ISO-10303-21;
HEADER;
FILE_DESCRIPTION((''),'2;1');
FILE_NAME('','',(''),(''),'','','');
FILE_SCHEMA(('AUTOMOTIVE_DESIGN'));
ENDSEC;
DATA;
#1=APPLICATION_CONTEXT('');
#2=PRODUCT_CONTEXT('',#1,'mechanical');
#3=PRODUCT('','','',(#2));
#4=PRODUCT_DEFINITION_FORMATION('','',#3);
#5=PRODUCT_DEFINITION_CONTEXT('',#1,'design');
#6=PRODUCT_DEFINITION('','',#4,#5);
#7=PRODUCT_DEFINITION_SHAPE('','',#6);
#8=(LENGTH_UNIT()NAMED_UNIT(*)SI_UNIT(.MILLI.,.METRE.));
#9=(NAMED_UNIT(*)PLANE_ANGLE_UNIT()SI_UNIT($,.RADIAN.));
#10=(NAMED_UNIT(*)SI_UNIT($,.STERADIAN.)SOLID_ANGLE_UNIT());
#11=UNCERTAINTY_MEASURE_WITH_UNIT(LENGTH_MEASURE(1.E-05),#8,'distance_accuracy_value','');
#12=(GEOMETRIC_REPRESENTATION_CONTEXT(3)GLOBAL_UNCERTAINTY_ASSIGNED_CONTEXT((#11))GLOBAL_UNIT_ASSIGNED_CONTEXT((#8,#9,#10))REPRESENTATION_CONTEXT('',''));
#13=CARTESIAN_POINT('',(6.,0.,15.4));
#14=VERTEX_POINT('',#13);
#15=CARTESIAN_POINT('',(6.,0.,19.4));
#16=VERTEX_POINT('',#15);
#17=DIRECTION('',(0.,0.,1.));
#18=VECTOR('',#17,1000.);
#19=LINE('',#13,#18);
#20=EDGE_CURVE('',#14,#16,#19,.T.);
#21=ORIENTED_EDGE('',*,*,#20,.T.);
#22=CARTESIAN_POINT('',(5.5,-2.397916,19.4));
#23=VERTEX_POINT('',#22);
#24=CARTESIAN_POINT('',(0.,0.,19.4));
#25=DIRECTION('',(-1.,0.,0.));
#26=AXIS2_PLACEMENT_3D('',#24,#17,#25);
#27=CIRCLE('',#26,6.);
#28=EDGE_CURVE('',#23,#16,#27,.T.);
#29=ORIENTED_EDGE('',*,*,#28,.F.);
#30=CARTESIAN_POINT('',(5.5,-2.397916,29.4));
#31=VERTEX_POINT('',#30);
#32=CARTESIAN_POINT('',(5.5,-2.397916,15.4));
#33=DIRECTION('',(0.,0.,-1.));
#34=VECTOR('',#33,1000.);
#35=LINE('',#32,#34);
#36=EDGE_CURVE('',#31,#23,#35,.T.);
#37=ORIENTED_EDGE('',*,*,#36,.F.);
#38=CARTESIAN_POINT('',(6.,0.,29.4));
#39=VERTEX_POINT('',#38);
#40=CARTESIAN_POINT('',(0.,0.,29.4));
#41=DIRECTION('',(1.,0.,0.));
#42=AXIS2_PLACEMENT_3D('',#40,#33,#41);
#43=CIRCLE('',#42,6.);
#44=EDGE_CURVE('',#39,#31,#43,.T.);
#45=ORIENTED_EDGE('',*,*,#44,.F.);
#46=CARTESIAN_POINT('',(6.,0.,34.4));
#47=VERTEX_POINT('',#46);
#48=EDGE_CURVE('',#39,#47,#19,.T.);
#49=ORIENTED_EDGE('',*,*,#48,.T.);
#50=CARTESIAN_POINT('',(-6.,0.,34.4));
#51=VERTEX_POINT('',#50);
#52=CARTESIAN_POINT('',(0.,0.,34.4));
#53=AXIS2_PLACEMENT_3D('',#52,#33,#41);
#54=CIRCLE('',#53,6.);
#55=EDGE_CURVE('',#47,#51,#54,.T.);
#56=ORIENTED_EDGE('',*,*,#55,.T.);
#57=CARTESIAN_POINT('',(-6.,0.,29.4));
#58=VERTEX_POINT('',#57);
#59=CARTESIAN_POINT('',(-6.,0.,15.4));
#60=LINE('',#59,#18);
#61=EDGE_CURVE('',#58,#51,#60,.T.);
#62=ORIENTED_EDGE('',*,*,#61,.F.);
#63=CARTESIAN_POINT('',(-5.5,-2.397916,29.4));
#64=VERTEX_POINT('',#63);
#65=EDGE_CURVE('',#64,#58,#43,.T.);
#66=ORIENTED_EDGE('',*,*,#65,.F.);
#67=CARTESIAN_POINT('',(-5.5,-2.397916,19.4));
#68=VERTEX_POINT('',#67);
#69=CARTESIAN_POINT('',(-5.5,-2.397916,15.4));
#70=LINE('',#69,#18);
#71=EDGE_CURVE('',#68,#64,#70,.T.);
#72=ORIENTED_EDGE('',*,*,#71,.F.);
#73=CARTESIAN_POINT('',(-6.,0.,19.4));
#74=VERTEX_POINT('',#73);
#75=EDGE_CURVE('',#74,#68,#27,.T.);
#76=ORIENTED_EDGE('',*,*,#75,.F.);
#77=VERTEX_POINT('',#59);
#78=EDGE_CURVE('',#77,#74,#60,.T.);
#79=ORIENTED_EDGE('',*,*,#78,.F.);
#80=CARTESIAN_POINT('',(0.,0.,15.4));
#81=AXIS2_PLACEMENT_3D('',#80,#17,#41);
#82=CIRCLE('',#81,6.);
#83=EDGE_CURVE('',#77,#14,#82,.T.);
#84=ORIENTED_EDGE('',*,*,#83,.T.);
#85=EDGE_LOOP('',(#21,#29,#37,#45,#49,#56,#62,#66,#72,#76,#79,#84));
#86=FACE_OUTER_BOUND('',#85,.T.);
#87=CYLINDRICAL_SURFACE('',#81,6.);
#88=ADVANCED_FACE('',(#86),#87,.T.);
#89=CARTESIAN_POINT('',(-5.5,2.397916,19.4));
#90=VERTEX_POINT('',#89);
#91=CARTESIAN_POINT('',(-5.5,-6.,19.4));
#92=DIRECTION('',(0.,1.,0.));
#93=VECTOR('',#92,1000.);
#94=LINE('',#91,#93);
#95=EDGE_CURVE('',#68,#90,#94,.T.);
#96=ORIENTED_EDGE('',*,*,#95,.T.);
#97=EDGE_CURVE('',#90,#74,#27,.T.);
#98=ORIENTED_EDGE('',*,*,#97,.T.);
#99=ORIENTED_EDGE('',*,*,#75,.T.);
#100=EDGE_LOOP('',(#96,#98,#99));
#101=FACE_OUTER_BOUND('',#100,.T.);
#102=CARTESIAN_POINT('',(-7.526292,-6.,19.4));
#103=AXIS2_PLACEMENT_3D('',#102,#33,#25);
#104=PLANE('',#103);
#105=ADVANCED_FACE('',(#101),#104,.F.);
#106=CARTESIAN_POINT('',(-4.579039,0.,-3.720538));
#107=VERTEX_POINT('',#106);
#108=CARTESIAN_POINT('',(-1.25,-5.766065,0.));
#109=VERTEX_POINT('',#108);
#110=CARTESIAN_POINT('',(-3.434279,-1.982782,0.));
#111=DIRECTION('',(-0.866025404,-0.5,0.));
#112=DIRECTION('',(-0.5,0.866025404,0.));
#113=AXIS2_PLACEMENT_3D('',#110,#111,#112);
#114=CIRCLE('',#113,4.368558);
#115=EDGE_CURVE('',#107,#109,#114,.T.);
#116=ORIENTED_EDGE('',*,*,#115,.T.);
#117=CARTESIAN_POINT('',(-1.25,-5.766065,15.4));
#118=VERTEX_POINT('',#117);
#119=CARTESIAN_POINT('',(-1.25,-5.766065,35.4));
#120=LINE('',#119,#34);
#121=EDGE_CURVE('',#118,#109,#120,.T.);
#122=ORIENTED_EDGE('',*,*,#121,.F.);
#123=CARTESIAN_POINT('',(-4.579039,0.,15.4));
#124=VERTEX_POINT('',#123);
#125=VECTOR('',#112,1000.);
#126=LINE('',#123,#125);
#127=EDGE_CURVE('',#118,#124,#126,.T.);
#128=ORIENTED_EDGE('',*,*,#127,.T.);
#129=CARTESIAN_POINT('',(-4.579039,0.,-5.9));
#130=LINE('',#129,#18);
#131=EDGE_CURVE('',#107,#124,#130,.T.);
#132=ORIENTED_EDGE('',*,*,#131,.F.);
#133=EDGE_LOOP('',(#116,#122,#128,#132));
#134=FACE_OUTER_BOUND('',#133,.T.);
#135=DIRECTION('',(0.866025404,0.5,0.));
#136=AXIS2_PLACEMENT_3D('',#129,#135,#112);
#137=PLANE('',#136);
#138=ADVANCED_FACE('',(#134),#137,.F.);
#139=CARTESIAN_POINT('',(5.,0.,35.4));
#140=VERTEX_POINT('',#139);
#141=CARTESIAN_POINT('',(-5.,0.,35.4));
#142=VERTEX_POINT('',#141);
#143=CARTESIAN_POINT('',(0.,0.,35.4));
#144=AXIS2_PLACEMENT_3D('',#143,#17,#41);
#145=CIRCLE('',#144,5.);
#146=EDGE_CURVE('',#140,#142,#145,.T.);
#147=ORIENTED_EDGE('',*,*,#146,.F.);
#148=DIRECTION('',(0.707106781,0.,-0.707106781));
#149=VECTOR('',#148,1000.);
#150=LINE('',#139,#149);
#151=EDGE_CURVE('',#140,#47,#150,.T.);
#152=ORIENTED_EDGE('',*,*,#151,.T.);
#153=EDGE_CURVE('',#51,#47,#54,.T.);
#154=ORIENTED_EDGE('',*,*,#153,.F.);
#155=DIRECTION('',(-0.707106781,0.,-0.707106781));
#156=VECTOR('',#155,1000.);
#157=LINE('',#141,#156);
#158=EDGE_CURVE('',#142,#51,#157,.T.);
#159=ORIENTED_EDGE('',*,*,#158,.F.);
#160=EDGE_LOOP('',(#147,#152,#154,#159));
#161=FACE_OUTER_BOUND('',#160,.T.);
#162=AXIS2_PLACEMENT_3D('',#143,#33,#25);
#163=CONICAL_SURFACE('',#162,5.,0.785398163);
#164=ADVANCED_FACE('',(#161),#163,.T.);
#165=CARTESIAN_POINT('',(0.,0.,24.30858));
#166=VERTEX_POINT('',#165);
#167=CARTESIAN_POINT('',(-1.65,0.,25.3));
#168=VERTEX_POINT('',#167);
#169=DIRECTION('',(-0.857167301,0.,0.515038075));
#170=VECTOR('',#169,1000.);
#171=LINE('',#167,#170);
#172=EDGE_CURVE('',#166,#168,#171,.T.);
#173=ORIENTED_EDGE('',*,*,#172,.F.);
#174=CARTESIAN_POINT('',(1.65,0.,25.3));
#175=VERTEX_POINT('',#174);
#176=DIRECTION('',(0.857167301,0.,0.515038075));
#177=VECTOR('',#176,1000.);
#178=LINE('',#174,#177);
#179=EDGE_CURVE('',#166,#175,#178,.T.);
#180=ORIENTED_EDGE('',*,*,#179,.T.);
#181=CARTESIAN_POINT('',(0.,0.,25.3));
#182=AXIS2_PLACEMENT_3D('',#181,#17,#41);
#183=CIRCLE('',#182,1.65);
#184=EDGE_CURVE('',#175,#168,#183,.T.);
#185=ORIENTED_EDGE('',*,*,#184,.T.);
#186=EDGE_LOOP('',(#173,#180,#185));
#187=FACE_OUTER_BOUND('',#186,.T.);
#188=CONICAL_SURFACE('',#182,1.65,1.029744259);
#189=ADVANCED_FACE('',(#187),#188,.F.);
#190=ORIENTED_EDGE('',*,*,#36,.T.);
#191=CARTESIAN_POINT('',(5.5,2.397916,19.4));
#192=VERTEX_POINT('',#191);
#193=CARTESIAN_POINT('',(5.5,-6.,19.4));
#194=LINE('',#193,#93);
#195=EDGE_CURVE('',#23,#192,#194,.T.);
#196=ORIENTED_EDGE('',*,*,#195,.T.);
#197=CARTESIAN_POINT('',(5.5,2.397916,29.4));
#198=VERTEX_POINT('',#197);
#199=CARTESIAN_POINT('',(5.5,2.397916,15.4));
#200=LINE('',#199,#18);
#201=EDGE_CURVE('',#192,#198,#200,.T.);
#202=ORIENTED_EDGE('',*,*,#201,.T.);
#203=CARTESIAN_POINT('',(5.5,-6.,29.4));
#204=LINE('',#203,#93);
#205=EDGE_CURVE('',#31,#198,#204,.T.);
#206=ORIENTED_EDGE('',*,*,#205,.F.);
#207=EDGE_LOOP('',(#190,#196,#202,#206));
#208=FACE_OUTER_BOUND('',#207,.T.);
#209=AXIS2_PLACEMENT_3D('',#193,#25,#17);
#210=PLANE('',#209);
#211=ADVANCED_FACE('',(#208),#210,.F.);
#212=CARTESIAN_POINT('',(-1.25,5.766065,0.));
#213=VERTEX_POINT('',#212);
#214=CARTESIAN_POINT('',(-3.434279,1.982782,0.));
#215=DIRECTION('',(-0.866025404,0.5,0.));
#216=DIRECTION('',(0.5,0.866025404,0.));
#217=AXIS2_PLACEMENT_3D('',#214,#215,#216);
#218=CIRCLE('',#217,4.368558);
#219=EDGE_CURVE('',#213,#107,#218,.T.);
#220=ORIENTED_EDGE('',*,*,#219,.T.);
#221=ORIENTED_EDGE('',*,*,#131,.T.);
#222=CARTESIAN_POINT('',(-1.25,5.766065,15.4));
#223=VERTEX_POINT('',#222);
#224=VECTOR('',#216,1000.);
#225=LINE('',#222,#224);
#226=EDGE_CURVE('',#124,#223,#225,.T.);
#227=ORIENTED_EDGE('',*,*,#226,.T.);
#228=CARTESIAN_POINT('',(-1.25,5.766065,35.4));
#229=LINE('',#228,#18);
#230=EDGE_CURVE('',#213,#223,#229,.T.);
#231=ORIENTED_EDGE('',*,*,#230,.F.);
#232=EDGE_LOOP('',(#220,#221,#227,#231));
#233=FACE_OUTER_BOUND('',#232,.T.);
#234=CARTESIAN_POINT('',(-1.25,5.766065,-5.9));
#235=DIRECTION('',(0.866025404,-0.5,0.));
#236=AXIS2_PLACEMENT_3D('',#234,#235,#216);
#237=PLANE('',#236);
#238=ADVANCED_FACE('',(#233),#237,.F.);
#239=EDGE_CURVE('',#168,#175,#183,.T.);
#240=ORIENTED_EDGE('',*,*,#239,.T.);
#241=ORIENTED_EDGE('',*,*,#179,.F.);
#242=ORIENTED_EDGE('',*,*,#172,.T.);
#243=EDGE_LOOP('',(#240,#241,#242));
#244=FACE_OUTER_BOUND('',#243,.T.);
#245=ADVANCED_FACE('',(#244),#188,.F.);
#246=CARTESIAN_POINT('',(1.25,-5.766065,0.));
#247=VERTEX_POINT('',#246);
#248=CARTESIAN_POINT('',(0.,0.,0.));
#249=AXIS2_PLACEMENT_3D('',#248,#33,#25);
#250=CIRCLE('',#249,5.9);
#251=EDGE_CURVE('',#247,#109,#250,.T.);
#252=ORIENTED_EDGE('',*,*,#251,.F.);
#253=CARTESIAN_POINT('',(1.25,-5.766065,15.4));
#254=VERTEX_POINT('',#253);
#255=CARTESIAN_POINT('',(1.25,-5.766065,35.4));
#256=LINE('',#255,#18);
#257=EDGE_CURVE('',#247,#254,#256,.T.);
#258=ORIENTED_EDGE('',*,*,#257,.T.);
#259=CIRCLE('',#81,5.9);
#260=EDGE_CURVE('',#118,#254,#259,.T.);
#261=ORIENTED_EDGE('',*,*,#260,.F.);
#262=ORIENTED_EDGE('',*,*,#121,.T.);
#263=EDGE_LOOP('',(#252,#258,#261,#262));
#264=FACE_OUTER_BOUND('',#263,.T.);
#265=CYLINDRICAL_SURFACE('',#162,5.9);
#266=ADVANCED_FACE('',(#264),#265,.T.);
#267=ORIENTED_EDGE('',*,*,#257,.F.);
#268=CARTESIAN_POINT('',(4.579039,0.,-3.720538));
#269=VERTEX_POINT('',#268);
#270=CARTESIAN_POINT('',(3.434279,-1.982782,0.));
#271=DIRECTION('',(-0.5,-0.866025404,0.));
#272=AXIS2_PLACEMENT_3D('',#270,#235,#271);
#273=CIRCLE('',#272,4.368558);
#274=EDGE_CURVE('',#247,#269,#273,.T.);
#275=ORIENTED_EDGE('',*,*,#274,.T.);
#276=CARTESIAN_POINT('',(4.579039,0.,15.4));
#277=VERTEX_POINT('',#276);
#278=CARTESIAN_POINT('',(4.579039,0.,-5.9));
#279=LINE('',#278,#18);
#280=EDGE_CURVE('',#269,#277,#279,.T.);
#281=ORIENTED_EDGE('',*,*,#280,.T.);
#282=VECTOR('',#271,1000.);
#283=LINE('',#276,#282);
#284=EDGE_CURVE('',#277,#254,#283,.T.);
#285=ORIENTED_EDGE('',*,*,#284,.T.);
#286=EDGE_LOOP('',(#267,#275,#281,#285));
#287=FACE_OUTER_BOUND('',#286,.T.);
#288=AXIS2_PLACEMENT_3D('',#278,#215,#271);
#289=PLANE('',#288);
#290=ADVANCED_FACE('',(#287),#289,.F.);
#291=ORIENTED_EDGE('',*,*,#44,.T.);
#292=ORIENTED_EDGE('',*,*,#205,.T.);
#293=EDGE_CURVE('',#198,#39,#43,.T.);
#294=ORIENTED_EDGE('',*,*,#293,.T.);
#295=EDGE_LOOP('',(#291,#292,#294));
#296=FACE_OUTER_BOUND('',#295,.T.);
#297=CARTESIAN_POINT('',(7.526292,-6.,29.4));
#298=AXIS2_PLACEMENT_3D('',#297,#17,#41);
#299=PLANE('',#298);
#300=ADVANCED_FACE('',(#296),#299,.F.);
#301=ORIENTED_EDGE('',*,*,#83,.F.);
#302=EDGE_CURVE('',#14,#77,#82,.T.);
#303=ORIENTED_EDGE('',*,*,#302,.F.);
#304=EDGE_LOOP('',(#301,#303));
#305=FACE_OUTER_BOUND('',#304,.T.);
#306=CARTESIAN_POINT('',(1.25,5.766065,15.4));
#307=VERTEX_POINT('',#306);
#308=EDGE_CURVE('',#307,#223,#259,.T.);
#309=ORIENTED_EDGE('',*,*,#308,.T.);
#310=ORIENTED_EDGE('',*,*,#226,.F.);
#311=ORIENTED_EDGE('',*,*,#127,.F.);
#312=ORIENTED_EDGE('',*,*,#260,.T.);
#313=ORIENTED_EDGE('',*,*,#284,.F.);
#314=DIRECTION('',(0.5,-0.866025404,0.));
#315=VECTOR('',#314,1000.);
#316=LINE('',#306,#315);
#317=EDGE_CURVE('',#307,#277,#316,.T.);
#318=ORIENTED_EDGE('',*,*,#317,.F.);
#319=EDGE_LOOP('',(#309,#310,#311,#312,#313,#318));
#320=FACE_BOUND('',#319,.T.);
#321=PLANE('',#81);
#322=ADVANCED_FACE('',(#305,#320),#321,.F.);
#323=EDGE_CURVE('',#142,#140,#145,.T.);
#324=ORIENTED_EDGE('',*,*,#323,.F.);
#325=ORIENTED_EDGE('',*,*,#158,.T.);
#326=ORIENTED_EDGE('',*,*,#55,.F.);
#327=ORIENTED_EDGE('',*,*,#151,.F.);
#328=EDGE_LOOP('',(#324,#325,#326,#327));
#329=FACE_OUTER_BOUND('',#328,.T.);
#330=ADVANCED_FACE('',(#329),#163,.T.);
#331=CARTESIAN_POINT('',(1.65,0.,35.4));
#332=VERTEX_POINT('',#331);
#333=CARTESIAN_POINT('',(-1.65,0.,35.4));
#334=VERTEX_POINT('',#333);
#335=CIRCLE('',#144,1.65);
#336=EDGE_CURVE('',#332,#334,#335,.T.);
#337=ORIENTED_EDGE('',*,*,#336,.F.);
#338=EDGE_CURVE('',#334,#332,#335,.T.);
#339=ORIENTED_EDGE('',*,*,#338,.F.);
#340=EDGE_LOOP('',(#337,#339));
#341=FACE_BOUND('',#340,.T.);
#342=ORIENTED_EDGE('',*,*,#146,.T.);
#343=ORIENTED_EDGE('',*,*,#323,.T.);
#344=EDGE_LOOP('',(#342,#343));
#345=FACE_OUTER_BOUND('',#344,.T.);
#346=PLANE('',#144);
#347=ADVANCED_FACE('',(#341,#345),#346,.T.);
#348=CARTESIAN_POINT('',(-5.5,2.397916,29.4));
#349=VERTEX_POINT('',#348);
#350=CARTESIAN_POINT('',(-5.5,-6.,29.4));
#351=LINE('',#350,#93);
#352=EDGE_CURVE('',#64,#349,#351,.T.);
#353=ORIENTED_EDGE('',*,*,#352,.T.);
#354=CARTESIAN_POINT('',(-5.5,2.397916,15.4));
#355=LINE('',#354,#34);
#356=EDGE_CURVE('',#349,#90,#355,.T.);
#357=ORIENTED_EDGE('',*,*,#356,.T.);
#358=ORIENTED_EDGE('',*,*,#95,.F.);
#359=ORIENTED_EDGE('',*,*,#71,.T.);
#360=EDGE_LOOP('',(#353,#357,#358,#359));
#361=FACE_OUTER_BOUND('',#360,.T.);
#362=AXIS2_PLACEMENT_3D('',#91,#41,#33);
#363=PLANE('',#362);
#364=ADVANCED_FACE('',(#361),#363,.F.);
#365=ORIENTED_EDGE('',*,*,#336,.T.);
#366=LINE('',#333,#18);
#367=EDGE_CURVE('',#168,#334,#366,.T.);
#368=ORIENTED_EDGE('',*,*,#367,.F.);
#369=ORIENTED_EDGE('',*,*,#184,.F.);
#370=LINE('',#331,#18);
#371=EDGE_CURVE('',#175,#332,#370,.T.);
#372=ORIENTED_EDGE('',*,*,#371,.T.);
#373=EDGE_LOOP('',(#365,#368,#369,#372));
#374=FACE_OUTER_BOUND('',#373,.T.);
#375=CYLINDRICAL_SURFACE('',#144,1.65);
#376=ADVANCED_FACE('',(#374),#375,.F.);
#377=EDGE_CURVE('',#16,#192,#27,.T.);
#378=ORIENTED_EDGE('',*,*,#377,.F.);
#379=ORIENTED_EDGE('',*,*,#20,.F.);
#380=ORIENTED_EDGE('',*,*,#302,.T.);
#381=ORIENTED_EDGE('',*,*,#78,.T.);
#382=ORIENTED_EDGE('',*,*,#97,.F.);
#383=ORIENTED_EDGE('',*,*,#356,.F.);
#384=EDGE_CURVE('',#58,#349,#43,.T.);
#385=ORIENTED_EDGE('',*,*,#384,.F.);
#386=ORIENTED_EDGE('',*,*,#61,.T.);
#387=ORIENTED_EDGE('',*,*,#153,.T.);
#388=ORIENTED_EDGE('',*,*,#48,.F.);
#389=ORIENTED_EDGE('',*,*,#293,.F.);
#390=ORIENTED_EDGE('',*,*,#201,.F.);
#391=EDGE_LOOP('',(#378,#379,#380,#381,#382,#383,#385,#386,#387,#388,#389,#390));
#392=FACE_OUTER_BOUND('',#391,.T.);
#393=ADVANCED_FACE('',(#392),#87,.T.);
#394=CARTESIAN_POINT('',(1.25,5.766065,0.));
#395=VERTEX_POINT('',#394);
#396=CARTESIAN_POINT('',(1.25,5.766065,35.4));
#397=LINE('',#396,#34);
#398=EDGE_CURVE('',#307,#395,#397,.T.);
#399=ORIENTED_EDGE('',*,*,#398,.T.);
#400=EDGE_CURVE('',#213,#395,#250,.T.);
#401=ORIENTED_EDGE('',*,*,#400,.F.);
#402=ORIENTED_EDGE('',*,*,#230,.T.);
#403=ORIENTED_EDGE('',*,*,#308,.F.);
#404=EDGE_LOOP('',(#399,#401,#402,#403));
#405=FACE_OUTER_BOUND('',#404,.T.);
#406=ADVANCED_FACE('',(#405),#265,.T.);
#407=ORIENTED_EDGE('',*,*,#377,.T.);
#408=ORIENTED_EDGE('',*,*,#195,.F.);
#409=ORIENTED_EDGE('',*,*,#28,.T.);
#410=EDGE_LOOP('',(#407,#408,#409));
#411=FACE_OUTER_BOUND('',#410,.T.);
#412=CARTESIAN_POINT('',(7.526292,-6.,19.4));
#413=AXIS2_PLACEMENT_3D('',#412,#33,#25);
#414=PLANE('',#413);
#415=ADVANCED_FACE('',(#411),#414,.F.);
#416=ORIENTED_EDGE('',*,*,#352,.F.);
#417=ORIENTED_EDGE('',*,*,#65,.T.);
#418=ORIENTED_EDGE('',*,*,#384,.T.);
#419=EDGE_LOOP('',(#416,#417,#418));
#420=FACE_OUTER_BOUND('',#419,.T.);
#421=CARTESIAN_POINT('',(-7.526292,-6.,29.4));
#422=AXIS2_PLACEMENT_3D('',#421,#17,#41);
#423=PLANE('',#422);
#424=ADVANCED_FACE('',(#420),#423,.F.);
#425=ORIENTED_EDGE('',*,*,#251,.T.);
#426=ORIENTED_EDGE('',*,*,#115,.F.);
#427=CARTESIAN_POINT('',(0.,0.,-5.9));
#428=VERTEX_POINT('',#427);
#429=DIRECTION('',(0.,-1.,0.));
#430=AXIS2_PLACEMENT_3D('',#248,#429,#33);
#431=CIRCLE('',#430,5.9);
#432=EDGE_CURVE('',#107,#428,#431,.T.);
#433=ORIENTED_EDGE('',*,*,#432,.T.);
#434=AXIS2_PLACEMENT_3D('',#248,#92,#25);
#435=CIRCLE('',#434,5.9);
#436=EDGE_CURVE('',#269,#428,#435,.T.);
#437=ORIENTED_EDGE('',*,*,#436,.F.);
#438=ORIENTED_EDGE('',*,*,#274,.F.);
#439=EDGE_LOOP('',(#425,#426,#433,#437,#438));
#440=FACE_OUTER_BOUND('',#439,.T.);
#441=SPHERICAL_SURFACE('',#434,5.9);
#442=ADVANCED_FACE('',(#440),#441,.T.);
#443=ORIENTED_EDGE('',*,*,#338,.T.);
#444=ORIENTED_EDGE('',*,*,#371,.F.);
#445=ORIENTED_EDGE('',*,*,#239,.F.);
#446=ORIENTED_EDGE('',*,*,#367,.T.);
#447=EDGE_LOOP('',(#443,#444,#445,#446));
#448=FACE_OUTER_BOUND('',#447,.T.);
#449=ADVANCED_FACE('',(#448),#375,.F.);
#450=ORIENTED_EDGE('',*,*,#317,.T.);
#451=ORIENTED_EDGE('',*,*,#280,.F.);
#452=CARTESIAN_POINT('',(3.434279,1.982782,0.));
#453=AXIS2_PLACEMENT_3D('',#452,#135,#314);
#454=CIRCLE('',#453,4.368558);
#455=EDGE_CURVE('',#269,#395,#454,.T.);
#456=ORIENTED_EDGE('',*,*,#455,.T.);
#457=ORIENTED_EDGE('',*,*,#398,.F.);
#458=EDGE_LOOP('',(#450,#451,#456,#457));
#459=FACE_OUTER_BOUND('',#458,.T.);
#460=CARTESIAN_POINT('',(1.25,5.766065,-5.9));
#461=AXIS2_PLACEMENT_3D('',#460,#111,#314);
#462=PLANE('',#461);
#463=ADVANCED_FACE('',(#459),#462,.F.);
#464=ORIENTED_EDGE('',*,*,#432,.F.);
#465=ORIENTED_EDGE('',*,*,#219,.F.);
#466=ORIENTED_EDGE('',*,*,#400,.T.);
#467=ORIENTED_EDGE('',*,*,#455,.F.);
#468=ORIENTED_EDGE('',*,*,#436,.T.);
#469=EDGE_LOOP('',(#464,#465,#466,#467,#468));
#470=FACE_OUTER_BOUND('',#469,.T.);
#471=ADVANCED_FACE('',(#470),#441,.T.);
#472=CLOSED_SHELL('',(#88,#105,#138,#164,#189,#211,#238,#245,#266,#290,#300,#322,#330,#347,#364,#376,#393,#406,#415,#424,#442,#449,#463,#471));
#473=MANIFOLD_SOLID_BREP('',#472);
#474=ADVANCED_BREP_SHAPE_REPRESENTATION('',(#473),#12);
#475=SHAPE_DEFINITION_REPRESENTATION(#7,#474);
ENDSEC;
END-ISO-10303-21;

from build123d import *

# Parameters (mm, degrees)
SKETCH1_R               = 5.9
BOSS_EXTRUDE1_DEPTH     = 35.4
M4_TAPPED_HOLE1_D       = 3.3
M4_TAPPED_HOLE1_DEPTH   = 10.1
M4_TAPPED_HOLE1_TIP     = 0.991420021
SKETCH5_R               = 6
SKETCH5_R_2             = 4
BOSS_EXTRUDE2_DEPTH     = 20
CHAMFER1_SIZE           = 1
CUT_EXTRUDE1_DEPTH      = 37.402747149
CUT_EXTRUDE1_DEPTH_BACK = 37.402747149
SKETCH6_W               = 2.026292368
SKETCH6_H               = 10
SKETCH7_OUTSIDE_W       = 22.93
SKETCH7_OUTSIDE_H       = 22.93
CUT_EXTRUDE2_DEPTH      = 23.927930565


with BuildPart() as part:
    # Sketch1 → Boss-Extrude1 (new body)
    with BuildSketch(Plane.XY):
        Circle(SKETCH1_R)
    extrude(amount=BOSS_EXTRUDE1_DEPTH)

    # Sketch2 → Revolve1 (revolve)
    with BuildSketch(Plane(origin=(0, 0, 0), x_dir=(1, 0, 0), z_dir=(0, 1, 0))):
        with BuildLine():
            Line((0, 5.9), (0, 0))
            Line((0, 0), (-5.9, 0))
            ThreePointArc((-5.9, 0), (-4.171930009, 4.171930009), (0, 5.9))
        make_face()
    revolve(axis=Axis((0, 0, -5.9), (0, 0, 1)))

    # M4 Tapped Hole1
    with Locations(Plane.XY.offset(35.4)):
        with Locations((0, 0)):
            Hole(M4_TAPPED_HOLE1_D / 2, depth=M4_TAPPED_HOLE1_DEPTH)
            with Locations((0, 0, -(M4_TAPPED_HOLE1_DEPTH + M4_TAPPED_HOLE1_TIP / 2))):  # 118° drill point
                Cone(0, M4_TAPPED_HOLE1_D / 2, M4_TAPPED_HOLE1_TIP, mode=Mode.SUBTRACT)

    # Sketch5 → Boss-Extrude2 (add)
    with BuildSketch(Plane.XY.offset(35.4)):
        Circle(SKETCH5_R)
        Circle(SKETCH5_R_2, mode=Mode.SUBTRACT)
    extrude(amount=-BOSS_EXTRUDE2_DEPTH)

    # Chamfer1
    chamfer1_edges = [part.edges().sort_by_distance(p)[0] for p in [
        (-6, 0, 35.4),
    ]]
    chamfer(chamfer1_edges, length=CHAMFER1_SIZE)

    # Sketch6 → Cut-Extrude1 (cut, two sides: drawn at the far end of the back side and taken through both)
    with BuildSketch(Plane(origin=(0, 0, 0), x_dir=(1, 0, 0), z_dir=(0, 1, 0)).offset(-CUT_EXTRUDE1_DEPTH_BACK)):
        with Locations((-6.513146184, -24.4)):
            Rectangle(SKETCH6_W, SKETCH6_H)
        with Locations((6.513146184, -24.4)):
            Rectangle(SKETCH6_W, SKETCH6_H)
    extrude(amount=CUT_EXTRUDE1_DEPTH + CUT_EXTRUDE1_DEPTH_BACK, mode=Mode.SUBTRACT)

    # Sketch7 outside → Cut-Extrude2 (cut, through all)
    with BuildSketch(Plane(origin=(0, 0, 15.4), x_dir=(-1, 0, 0), z_dir=(0, 0, -1))):
        Rectangle(SKETCH7_OUTSIDE_W, SKETCH7_OUTSIDE_H)
        with BuildLine():
            Line((-1.25, 5.766064516), (-4.5790389, 0))
            Line((-4.5790389, 0), (-1.25, -5.766064516))
            ThreePointArc((-1.25, -5.766064516), (0, -5.9), (1.25, -5.766064516))
            Line((1.25, -5.766064516), (4.5790389, 0))
            Line((4.5790389, 0), (1.25, 5.766064516))
            ThreePointArc((1.25, 5.766064516), (0, 5.9), (-1.25, 5.766064516))
        make_face(mode=Mode.SUBTRACT)
    extrude(amount=CUT_EXTRUDE2_DEPTH, mode=Mode.SUBTRACT)


solid = part.part
